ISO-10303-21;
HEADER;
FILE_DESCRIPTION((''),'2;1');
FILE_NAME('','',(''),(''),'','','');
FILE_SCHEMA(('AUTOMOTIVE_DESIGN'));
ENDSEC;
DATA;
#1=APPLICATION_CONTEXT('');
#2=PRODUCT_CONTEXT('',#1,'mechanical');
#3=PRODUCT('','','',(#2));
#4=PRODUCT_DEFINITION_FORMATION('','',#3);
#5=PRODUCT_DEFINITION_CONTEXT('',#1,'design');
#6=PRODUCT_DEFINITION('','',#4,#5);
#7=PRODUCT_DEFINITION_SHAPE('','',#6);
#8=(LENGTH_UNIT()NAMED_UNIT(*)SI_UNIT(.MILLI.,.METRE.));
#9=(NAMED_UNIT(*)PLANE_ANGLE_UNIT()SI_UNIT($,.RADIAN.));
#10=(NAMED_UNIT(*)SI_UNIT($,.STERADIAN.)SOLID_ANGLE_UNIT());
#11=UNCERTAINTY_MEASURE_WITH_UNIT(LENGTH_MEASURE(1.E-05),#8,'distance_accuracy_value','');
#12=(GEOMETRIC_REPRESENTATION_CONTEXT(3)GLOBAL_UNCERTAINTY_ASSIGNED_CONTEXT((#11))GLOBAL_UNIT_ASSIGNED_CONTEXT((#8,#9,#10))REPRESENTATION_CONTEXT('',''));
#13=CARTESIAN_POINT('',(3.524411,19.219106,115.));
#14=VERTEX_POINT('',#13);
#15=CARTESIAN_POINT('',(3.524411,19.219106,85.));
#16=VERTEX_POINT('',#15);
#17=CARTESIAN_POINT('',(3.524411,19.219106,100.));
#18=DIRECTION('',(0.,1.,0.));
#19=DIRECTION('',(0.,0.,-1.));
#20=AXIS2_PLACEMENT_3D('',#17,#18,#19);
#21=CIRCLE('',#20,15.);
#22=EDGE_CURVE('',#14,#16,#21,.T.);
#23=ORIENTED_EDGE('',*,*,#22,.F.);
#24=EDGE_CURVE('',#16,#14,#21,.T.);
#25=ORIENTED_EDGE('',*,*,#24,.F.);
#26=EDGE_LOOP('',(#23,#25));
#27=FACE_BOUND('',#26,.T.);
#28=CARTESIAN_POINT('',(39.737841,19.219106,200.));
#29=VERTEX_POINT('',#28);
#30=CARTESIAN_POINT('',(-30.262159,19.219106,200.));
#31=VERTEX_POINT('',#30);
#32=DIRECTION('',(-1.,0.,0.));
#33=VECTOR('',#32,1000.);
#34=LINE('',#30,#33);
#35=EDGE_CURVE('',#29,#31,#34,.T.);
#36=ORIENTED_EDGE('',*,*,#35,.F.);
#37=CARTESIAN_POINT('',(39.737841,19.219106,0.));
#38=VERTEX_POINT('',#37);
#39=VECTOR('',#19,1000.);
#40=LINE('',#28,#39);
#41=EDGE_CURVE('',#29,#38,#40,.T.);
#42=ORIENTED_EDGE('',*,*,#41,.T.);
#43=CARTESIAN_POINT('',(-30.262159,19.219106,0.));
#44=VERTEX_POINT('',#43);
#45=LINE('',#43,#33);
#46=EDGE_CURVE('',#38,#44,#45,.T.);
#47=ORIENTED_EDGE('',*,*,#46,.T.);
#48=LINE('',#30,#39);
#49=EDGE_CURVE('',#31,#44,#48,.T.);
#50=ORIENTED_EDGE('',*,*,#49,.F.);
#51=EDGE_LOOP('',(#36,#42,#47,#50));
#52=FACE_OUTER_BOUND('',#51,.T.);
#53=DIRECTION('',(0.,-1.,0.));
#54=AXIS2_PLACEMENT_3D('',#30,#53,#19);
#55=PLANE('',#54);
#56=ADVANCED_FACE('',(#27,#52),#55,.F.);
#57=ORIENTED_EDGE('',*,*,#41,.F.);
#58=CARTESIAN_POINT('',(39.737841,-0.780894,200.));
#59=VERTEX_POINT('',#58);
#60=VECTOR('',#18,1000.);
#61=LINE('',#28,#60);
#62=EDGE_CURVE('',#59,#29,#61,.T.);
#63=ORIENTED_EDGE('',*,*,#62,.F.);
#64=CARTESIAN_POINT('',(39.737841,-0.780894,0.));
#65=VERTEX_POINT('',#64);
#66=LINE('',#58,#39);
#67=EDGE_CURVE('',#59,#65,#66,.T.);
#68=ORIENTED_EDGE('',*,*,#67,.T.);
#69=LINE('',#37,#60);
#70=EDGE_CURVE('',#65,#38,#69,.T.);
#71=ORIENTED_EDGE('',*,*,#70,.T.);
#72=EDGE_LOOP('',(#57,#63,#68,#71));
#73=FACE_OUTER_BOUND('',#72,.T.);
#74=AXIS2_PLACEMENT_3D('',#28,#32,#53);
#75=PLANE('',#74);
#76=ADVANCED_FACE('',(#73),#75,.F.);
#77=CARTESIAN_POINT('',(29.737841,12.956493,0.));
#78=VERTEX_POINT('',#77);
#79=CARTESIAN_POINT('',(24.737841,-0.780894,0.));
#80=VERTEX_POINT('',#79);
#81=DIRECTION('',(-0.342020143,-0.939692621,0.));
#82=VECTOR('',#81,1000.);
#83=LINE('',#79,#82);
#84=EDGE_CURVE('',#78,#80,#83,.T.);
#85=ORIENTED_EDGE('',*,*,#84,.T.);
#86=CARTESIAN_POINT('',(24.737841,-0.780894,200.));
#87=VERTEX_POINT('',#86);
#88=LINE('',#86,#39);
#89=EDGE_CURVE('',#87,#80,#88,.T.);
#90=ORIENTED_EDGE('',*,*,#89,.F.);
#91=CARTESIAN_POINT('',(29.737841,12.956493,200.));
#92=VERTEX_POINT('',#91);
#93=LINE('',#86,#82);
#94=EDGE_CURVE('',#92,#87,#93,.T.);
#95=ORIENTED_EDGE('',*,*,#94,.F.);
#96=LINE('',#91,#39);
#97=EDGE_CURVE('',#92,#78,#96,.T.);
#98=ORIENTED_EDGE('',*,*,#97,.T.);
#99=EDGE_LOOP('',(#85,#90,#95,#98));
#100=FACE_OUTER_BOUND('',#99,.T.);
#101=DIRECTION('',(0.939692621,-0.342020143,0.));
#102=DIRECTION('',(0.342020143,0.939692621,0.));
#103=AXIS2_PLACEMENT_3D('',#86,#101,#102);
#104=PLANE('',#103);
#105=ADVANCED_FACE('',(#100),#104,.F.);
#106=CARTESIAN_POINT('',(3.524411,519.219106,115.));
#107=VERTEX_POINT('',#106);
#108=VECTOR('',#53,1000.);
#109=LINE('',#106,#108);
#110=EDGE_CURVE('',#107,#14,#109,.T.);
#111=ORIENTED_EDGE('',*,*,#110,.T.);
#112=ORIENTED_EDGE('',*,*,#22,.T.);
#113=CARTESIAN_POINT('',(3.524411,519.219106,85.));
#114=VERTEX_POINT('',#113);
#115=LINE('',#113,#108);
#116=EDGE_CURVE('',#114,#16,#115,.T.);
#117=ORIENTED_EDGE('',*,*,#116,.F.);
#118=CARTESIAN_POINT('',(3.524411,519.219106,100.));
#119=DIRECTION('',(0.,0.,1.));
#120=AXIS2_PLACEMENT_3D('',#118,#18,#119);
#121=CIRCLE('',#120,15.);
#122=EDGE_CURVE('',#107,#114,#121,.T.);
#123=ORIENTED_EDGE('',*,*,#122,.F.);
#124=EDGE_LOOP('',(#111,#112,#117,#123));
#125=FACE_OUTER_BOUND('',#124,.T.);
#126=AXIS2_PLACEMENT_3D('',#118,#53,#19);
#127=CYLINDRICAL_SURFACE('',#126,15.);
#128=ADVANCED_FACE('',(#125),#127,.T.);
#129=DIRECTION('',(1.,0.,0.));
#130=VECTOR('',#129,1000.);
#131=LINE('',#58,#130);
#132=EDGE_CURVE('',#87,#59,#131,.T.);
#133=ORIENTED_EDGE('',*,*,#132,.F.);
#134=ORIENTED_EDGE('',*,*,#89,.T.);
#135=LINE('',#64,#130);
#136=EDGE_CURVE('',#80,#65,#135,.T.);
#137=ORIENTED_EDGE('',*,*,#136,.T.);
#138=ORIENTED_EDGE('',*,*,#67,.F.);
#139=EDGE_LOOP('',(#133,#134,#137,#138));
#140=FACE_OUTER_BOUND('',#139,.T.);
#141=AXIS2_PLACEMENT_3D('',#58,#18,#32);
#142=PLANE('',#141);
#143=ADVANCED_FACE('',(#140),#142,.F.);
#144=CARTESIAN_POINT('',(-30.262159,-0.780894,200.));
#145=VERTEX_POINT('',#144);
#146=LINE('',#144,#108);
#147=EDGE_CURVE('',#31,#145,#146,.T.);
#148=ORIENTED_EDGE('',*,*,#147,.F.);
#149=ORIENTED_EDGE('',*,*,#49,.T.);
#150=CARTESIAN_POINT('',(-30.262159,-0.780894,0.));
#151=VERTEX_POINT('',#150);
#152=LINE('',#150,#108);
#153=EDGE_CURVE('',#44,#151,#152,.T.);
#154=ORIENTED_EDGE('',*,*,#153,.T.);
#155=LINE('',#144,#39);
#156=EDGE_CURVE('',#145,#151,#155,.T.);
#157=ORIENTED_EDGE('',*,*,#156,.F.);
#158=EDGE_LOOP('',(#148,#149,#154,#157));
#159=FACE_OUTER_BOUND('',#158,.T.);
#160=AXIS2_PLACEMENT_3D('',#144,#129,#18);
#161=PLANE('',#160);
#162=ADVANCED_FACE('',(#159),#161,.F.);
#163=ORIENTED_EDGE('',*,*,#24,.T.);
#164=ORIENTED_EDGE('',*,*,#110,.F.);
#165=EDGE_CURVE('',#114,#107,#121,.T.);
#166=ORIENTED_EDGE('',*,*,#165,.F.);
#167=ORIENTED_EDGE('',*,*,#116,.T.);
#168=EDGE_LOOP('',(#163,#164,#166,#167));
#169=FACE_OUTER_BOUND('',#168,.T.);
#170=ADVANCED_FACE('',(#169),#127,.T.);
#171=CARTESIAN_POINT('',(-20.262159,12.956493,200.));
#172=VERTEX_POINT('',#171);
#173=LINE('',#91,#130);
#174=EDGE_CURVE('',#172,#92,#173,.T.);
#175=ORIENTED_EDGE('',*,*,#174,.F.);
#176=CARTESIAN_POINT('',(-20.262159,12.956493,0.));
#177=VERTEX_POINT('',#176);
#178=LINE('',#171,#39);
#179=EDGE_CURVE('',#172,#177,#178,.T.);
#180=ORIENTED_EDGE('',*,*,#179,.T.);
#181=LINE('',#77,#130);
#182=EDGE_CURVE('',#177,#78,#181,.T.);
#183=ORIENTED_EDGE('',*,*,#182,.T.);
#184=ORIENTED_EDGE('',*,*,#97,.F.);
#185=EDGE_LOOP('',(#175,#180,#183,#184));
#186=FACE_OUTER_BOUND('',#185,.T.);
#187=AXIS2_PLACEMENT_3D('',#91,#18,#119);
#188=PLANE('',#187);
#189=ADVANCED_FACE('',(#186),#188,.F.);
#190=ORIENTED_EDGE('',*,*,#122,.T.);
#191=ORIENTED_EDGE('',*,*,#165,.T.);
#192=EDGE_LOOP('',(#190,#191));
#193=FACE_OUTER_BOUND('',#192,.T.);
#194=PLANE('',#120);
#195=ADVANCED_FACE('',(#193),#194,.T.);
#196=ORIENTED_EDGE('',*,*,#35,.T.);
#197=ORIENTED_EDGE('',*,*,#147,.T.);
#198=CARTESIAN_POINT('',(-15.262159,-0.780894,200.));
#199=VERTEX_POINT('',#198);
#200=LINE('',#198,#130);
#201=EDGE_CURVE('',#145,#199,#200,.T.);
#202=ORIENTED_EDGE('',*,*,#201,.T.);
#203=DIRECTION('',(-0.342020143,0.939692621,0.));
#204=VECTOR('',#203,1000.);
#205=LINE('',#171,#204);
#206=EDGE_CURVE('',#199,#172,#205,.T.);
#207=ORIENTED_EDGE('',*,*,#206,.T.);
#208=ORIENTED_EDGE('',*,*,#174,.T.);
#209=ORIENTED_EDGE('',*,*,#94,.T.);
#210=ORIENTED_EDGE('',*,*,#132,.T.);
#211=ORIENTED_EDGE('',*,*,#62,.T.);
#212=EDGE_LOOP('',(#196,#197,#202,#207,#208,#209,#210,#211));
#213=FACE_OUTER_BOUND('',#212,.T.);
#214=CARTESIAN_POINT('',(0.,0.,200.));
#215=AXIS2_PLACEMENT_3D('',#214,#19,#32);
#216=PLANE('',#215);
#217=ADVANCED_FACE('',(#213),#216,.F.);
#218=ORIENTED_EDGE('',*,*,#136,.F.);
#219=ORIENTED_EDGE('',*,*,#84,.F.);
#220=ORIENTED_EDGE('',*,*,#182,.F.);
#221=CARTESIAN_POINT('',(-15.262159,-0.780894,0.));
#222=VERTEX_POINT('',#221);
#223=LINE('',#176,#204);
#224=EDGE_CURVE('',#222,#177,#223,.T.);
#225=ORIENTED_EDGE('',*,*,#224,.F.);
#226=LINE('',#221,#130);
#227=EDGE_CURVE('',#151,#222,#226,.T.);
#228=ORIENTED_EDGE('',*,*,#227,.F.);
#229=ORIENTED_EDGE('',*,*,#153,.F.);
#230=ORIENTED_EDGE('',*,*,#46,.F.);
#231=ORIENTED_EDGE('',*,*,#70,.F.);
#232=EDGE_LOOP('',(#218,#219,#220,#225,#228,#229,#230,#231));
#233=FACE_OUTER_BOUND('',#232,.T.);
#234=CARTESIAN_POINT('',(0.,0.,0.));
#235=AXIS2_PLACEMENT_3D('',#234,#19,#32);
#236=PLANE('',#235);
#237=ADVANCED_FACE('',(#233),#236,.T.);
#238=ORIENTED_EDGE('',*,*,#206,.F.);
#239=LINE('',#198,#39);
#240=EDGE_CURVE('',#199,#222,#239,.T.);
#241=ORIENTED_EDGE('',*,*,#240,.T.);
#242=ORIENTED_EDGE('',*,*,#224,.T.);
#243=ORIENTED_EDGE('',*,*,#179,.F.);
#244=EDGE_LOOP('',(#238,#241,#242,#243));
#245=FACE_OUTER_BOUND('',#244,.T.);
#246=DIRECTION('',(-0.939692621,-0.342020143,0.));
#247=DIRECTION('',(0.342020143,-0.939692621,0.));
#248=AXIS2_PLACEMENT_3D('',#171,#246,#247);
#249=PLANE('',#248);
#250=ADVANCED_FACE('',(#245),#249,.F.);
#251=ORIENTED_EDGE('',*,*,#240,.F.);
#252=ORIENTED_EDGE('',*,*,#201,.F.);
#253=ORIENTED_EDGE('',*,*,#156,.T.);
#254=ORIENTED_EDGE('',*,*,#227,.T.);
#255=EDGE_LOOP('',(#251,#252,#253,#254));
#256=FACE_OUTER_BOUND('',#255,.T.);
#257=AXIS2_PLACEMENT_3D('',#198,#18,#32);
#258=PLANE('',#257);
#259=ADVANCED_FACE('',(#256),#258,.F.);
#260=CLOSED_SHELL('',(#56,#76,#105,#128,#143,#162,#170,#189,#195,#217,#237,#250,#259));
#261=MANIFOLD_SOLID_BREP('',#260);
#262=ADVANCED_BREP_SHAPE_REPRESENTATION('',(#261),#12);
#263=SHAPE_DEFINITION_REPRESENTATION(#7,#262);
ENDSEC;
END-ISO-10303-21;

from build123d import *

# Parameters (mm, degrees)
BOSS_EXTRUDE1_DEPTH = 200
SKETCH2_R           = 15
BOSS_EXTRUDE2_DEPTH = 500


with BuildPart() as part:
    # Sketch1 → Boss-Extrude1 (new body)
    with BuildSketch(Plane.XY):
        Polygon((-30.262159038, 19.219105843), (39.737840962, 19.219105843), (39.737840962, -0.780894157), (24.737840962, -0.780894157), (29.737840962, 12.95649294), (-20.262159038, 12.95649294), (-15.262159038, -0.780894157), (-30.262159038, -0.780894157), align=None)
    extrude(amount=BOSS_EXTRUDE1_DEPTH)

    # Sketch2 → Boss-Extrude2 (add)
    with BuildSketch(Plane(origin=(0, 19.219105843, 0), x_dir=(1, 0, 0), z_dir=(0, 1, 0))):
        with Locations(Location((3.524411209, -100, 0), (0, 0, 90))):
            Circle(SKETCH2_R)
    extrude(amount=BOSS_EXTRUDE2_DEPTH)


solid = part.part
